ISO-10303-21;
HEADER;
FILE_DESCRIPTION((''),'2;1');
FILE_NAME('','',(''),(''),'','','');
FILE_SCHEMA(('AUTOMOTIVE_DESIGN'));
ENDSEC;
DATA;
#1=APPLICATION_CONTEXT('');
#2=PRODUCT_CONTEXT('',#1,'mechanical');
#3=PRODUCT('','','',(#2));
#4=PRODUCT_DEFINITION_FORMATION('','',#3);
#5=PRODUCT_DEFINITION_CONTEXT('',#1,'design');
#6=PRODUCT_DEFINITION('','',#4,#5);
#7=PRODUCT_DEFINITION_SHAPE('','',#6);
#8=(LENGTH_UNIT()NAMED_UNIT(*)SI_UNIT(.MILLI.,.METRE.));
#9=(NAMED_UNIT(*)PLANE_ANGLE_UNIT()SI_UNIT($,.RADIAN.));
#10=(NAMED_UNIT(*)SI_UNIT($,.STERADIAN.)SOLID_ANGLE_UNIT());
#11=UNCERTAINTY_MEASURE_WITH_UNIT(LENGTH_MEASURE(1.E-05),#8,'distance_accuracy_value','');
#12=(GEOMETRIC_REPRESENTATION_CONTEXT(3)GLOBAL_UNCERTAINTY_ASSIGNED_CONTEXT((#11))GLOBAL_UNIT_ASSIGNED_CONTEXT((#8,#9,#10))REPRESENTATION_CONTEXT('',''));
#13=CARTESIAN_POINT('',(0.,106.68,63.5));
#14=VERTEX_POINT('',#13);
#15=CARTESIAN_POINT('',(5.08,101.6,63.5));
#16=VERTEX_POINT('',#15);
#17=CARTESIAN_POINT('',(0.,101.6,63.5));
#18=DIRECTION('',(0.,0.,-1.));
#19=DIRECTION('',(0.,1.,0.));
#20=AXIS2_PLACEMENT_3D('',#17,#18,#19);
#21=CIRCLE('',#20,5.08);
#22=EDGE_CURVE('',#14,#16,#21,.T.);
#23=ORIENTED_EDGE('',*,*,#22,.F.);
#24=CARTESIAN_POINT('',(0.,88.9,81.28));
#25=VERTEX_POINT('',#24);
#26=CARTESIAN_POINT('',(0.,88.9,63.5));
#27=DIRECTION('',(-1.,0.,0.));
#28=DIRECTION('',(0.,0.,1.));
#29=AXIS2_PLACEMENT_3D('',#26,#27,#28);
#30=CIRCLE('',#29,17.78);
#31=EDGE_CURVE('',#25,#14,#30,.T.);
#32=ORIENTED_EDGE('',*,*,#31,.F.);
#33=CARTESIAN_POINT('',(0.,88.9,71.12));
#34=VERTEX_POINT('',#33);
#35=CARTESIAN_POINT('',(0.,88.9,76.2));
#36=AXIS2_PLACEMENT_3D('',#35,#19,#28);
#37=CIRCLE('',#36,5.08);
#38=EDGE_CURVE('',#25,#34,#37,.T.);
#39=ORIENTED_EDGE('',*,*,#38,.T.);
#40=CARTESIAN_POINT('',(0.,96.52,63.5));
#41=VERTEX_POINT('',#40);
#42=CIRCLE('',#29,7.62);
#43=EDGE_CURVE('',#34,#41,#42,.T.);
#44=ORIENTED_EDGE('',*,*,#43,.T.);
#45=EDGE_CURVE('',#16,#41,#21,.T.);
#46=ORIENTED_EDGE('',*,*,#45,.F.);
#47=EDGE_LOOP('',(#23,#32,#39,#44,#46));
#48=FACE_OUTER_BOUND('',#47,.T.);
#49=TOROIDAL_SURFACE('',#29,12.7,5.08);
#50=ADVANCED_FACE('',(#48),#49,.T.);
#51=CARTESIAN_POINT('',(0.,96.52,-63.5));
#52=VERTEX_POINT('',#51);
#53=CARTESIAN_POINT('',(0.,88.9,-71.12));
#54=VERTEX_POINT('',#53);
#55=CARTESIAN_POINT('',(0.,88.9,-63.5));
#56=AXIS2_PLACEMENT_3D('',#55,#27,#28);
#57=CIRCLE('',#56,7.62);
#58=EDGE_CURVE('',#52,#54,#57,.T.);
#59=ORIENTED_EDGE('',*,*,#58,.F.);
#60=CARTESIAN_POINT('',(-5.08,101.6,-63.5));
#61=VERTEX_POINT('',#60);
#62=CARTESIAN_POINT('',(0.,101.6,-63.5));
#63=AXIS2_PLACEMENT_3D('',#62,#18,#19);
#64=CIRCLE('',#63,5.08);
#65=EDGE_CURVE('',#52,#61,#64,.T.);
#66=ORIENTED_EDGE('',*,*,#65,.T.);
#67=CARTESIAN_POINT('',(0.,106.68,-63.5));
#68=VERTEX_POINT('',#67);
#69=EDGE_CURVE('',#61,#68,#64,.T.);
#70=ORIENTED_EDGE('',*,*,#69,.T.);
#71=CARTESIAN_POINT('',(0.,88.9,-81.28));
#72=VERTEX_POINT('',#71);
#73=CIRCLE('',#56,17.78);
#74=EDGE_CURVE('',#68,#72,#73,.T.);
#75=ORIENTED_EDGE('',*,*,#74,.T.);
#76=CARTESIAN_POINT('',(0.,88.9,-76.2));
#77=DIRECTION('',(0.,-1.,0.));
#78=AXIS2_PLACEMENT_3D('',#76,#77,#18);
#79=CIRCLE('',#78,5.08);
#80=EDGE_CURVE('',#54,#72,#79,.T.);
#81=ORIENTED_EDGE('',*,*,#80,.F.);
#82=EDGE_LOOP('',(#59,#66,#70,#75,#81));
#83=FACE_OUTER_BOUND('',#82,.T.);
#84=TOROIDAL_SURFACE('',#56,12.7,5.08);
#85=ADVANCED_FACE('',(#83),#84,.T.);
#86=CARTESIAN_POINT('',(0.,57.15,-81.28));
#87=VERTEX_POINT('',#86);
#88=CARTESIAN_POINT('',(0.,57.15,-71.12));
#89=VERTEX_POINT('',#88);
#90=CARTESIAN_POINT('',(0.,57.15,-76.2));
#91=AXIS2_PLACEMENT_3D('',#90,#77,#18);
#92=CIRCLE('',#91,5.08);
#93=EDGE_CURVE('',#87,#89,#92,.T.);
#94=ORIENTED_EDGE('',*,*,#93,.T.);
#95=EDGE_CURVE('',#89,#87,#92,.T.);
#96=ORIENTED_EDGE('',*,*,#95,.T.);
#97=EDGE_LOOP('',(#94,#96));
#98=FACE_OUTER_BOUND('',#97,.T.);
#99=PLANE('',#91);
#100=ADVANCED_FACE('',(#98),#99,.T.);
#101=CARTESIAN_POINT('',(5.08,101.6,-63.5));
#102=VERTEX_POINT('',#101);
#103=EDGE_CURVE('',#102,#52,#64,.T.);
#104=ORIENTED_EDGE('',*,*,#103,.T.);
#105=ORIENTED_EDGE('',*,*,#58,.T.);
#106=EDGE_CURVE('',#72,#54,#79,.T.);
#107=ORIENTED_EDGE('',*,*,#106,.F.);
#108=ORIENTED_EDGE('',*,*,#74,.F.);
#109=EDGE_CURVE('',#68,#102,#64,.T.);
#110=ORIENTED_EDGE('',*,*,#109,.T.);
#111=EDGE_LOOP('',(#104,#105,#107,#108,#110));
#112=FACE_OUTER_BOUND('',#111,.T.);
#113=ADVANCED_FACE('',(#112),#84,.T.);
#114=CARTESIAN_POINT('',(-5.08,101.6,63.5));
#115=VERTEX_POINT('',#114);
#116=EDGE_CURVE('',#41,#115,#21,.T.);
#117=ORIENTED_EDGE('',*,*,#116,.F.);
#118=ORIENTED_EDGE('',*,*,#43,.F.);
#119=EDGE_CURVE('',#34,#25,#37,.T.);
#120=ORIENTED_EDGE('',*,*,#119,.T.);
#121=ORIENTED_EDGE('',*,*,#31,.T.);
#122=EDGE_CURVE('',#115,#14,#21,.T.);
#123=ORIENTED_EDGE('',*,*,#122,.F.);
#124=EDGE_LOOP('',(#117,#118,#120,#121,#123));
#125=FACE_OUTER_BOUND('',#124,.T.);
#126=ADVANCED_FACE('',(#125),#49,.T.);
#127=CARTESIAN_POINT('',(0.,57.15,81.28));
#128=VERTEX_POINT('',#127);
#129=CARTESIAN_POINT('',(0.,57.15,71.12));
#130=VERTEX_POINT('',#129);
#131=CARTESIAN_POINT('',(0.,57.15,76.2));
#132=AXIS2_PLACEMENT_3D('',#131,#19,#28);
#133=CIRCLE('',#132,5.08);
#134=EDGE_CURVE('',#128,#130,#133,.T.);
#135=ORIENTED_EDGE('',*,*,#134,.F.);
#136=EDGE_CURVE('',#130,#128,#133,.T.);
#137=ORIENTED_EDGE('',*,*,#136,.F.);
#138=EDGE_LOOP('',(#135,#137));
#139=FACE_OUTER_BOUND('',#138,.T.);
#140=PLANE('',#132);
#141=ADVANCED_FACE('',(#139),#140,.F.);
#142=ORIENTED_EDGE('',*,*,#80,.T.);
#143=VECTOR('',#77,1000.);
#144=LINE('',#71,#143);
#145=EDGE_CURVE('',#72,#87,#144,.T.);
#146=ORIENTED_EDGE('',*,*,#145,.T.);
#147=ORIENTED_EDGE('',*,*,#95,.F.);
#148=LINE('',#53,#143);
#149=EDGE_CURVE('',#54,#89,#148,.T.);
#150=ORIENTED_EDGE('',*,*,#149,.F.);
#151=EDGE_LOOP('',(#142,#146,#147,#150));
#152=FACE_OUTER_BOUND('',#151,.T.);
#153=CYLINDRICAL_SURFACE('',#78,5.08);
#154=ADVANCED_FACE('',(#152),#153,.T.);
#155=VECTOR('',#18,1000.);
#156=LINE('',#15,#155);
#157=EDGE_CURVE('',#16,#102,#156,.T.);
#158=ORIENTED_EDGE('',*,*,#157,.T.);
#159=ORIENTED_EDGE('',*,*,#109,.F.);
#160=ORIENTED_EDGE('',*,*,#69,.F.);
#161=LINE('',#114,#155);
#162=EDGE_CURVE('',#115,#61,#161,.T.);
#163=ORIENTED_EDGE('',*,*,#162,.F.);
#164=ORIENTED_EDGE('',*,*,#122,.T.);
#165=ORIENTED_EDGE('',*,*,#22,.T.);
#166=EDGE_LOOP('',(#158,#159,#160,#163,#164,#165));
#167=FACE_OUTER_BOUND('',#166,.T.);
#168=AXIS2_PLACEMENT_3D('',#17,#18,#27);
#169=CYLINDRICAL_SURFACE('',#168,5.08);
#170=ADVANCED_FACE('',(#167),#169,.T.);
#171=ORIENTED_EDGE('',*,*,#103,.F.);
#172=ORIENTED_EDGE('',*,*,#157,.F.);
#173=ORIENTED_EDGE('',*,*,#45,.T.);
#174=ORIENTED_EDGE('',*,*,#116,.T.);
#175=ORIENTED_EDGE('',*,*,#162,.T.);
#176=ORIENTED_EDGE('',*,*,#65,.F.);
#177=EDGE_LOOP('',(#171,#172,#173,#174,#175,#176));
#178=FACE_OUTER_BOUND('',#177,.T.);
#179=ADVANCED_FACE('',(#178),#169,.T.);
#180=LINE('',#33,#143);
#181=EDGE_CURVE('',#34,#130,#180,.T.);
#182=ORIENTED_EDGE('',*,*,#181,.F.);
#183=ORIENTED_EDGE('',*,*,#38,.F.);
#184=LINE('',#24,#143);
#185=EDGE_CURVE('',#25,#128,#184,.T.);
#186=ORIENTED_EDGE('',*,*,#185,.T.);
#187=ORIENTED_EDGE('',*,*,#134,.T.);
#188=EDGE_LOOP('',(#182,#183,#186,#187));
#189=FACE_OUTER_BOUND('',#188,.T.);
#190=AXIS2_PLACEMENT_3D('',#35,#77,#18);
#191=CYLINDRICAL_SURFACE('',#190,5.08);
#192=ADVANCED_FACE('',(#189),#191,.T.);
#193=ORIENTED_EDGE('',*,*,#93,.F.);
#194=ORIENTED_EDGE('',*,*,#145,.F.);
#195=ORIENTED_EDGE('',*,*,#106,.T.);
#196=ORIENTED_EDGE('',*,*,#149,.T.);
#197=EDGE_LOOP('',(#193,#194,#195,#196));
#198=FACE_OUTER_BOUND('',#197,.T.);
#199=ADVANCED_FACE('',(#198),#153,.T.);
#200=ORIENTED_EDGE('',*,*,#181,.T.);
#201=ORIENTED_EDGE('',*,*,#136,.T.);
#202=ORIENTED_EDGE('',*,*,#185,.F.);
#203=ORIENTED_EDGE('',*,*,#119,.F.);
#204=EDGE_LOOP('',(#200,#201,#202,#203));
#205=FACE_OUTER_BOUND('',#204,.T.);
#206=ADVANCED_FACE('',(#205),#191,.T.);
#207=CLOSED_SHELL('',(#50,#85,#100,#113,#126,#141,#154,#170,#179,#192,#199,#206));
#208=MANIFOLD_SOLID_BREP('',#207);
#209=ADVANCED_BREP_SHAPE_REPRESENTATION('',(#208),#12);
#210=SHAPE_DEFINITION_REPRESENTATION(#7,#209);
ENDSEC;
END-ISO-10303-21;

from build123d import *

# Parameters (mm, degrees)
SKETCH2_R = 5.08


with BuildPart() as part:
    # Sweep1: sweep along a path in Sketch1
    with BuildLine(Plane(origin=(0, 0, 0), x_dir=(0, 0, -1), z_dir=(1, 0, 0))) as sweep1_path:
        Line((-76.2, 57.15), (-76.2, 88.9))
        ThreePointArc((-76.2, 88.9), (-72.480256121, 97.880256121), (-63.5, 101.6))
        Line((-63.5, 101.6), (63.5, 101.6))
        ThreePointArc((63.5, 101.6), (72.480256121, 97.880256121), (76.2, 88.9))
        Line((76.2, 88.9), (76.2, 57.15))
    # Sketch2 → Sweep1 (sweep)
    with BuildSketch(Plane(origin=(0, 57.15, 76.2), x_dir=(-1, 0, 0), z_dir=(0, 1, 0))):
        Circle(SKETCH2_R)
    sweep(path=sweep1_path.line)


solid = part.part
